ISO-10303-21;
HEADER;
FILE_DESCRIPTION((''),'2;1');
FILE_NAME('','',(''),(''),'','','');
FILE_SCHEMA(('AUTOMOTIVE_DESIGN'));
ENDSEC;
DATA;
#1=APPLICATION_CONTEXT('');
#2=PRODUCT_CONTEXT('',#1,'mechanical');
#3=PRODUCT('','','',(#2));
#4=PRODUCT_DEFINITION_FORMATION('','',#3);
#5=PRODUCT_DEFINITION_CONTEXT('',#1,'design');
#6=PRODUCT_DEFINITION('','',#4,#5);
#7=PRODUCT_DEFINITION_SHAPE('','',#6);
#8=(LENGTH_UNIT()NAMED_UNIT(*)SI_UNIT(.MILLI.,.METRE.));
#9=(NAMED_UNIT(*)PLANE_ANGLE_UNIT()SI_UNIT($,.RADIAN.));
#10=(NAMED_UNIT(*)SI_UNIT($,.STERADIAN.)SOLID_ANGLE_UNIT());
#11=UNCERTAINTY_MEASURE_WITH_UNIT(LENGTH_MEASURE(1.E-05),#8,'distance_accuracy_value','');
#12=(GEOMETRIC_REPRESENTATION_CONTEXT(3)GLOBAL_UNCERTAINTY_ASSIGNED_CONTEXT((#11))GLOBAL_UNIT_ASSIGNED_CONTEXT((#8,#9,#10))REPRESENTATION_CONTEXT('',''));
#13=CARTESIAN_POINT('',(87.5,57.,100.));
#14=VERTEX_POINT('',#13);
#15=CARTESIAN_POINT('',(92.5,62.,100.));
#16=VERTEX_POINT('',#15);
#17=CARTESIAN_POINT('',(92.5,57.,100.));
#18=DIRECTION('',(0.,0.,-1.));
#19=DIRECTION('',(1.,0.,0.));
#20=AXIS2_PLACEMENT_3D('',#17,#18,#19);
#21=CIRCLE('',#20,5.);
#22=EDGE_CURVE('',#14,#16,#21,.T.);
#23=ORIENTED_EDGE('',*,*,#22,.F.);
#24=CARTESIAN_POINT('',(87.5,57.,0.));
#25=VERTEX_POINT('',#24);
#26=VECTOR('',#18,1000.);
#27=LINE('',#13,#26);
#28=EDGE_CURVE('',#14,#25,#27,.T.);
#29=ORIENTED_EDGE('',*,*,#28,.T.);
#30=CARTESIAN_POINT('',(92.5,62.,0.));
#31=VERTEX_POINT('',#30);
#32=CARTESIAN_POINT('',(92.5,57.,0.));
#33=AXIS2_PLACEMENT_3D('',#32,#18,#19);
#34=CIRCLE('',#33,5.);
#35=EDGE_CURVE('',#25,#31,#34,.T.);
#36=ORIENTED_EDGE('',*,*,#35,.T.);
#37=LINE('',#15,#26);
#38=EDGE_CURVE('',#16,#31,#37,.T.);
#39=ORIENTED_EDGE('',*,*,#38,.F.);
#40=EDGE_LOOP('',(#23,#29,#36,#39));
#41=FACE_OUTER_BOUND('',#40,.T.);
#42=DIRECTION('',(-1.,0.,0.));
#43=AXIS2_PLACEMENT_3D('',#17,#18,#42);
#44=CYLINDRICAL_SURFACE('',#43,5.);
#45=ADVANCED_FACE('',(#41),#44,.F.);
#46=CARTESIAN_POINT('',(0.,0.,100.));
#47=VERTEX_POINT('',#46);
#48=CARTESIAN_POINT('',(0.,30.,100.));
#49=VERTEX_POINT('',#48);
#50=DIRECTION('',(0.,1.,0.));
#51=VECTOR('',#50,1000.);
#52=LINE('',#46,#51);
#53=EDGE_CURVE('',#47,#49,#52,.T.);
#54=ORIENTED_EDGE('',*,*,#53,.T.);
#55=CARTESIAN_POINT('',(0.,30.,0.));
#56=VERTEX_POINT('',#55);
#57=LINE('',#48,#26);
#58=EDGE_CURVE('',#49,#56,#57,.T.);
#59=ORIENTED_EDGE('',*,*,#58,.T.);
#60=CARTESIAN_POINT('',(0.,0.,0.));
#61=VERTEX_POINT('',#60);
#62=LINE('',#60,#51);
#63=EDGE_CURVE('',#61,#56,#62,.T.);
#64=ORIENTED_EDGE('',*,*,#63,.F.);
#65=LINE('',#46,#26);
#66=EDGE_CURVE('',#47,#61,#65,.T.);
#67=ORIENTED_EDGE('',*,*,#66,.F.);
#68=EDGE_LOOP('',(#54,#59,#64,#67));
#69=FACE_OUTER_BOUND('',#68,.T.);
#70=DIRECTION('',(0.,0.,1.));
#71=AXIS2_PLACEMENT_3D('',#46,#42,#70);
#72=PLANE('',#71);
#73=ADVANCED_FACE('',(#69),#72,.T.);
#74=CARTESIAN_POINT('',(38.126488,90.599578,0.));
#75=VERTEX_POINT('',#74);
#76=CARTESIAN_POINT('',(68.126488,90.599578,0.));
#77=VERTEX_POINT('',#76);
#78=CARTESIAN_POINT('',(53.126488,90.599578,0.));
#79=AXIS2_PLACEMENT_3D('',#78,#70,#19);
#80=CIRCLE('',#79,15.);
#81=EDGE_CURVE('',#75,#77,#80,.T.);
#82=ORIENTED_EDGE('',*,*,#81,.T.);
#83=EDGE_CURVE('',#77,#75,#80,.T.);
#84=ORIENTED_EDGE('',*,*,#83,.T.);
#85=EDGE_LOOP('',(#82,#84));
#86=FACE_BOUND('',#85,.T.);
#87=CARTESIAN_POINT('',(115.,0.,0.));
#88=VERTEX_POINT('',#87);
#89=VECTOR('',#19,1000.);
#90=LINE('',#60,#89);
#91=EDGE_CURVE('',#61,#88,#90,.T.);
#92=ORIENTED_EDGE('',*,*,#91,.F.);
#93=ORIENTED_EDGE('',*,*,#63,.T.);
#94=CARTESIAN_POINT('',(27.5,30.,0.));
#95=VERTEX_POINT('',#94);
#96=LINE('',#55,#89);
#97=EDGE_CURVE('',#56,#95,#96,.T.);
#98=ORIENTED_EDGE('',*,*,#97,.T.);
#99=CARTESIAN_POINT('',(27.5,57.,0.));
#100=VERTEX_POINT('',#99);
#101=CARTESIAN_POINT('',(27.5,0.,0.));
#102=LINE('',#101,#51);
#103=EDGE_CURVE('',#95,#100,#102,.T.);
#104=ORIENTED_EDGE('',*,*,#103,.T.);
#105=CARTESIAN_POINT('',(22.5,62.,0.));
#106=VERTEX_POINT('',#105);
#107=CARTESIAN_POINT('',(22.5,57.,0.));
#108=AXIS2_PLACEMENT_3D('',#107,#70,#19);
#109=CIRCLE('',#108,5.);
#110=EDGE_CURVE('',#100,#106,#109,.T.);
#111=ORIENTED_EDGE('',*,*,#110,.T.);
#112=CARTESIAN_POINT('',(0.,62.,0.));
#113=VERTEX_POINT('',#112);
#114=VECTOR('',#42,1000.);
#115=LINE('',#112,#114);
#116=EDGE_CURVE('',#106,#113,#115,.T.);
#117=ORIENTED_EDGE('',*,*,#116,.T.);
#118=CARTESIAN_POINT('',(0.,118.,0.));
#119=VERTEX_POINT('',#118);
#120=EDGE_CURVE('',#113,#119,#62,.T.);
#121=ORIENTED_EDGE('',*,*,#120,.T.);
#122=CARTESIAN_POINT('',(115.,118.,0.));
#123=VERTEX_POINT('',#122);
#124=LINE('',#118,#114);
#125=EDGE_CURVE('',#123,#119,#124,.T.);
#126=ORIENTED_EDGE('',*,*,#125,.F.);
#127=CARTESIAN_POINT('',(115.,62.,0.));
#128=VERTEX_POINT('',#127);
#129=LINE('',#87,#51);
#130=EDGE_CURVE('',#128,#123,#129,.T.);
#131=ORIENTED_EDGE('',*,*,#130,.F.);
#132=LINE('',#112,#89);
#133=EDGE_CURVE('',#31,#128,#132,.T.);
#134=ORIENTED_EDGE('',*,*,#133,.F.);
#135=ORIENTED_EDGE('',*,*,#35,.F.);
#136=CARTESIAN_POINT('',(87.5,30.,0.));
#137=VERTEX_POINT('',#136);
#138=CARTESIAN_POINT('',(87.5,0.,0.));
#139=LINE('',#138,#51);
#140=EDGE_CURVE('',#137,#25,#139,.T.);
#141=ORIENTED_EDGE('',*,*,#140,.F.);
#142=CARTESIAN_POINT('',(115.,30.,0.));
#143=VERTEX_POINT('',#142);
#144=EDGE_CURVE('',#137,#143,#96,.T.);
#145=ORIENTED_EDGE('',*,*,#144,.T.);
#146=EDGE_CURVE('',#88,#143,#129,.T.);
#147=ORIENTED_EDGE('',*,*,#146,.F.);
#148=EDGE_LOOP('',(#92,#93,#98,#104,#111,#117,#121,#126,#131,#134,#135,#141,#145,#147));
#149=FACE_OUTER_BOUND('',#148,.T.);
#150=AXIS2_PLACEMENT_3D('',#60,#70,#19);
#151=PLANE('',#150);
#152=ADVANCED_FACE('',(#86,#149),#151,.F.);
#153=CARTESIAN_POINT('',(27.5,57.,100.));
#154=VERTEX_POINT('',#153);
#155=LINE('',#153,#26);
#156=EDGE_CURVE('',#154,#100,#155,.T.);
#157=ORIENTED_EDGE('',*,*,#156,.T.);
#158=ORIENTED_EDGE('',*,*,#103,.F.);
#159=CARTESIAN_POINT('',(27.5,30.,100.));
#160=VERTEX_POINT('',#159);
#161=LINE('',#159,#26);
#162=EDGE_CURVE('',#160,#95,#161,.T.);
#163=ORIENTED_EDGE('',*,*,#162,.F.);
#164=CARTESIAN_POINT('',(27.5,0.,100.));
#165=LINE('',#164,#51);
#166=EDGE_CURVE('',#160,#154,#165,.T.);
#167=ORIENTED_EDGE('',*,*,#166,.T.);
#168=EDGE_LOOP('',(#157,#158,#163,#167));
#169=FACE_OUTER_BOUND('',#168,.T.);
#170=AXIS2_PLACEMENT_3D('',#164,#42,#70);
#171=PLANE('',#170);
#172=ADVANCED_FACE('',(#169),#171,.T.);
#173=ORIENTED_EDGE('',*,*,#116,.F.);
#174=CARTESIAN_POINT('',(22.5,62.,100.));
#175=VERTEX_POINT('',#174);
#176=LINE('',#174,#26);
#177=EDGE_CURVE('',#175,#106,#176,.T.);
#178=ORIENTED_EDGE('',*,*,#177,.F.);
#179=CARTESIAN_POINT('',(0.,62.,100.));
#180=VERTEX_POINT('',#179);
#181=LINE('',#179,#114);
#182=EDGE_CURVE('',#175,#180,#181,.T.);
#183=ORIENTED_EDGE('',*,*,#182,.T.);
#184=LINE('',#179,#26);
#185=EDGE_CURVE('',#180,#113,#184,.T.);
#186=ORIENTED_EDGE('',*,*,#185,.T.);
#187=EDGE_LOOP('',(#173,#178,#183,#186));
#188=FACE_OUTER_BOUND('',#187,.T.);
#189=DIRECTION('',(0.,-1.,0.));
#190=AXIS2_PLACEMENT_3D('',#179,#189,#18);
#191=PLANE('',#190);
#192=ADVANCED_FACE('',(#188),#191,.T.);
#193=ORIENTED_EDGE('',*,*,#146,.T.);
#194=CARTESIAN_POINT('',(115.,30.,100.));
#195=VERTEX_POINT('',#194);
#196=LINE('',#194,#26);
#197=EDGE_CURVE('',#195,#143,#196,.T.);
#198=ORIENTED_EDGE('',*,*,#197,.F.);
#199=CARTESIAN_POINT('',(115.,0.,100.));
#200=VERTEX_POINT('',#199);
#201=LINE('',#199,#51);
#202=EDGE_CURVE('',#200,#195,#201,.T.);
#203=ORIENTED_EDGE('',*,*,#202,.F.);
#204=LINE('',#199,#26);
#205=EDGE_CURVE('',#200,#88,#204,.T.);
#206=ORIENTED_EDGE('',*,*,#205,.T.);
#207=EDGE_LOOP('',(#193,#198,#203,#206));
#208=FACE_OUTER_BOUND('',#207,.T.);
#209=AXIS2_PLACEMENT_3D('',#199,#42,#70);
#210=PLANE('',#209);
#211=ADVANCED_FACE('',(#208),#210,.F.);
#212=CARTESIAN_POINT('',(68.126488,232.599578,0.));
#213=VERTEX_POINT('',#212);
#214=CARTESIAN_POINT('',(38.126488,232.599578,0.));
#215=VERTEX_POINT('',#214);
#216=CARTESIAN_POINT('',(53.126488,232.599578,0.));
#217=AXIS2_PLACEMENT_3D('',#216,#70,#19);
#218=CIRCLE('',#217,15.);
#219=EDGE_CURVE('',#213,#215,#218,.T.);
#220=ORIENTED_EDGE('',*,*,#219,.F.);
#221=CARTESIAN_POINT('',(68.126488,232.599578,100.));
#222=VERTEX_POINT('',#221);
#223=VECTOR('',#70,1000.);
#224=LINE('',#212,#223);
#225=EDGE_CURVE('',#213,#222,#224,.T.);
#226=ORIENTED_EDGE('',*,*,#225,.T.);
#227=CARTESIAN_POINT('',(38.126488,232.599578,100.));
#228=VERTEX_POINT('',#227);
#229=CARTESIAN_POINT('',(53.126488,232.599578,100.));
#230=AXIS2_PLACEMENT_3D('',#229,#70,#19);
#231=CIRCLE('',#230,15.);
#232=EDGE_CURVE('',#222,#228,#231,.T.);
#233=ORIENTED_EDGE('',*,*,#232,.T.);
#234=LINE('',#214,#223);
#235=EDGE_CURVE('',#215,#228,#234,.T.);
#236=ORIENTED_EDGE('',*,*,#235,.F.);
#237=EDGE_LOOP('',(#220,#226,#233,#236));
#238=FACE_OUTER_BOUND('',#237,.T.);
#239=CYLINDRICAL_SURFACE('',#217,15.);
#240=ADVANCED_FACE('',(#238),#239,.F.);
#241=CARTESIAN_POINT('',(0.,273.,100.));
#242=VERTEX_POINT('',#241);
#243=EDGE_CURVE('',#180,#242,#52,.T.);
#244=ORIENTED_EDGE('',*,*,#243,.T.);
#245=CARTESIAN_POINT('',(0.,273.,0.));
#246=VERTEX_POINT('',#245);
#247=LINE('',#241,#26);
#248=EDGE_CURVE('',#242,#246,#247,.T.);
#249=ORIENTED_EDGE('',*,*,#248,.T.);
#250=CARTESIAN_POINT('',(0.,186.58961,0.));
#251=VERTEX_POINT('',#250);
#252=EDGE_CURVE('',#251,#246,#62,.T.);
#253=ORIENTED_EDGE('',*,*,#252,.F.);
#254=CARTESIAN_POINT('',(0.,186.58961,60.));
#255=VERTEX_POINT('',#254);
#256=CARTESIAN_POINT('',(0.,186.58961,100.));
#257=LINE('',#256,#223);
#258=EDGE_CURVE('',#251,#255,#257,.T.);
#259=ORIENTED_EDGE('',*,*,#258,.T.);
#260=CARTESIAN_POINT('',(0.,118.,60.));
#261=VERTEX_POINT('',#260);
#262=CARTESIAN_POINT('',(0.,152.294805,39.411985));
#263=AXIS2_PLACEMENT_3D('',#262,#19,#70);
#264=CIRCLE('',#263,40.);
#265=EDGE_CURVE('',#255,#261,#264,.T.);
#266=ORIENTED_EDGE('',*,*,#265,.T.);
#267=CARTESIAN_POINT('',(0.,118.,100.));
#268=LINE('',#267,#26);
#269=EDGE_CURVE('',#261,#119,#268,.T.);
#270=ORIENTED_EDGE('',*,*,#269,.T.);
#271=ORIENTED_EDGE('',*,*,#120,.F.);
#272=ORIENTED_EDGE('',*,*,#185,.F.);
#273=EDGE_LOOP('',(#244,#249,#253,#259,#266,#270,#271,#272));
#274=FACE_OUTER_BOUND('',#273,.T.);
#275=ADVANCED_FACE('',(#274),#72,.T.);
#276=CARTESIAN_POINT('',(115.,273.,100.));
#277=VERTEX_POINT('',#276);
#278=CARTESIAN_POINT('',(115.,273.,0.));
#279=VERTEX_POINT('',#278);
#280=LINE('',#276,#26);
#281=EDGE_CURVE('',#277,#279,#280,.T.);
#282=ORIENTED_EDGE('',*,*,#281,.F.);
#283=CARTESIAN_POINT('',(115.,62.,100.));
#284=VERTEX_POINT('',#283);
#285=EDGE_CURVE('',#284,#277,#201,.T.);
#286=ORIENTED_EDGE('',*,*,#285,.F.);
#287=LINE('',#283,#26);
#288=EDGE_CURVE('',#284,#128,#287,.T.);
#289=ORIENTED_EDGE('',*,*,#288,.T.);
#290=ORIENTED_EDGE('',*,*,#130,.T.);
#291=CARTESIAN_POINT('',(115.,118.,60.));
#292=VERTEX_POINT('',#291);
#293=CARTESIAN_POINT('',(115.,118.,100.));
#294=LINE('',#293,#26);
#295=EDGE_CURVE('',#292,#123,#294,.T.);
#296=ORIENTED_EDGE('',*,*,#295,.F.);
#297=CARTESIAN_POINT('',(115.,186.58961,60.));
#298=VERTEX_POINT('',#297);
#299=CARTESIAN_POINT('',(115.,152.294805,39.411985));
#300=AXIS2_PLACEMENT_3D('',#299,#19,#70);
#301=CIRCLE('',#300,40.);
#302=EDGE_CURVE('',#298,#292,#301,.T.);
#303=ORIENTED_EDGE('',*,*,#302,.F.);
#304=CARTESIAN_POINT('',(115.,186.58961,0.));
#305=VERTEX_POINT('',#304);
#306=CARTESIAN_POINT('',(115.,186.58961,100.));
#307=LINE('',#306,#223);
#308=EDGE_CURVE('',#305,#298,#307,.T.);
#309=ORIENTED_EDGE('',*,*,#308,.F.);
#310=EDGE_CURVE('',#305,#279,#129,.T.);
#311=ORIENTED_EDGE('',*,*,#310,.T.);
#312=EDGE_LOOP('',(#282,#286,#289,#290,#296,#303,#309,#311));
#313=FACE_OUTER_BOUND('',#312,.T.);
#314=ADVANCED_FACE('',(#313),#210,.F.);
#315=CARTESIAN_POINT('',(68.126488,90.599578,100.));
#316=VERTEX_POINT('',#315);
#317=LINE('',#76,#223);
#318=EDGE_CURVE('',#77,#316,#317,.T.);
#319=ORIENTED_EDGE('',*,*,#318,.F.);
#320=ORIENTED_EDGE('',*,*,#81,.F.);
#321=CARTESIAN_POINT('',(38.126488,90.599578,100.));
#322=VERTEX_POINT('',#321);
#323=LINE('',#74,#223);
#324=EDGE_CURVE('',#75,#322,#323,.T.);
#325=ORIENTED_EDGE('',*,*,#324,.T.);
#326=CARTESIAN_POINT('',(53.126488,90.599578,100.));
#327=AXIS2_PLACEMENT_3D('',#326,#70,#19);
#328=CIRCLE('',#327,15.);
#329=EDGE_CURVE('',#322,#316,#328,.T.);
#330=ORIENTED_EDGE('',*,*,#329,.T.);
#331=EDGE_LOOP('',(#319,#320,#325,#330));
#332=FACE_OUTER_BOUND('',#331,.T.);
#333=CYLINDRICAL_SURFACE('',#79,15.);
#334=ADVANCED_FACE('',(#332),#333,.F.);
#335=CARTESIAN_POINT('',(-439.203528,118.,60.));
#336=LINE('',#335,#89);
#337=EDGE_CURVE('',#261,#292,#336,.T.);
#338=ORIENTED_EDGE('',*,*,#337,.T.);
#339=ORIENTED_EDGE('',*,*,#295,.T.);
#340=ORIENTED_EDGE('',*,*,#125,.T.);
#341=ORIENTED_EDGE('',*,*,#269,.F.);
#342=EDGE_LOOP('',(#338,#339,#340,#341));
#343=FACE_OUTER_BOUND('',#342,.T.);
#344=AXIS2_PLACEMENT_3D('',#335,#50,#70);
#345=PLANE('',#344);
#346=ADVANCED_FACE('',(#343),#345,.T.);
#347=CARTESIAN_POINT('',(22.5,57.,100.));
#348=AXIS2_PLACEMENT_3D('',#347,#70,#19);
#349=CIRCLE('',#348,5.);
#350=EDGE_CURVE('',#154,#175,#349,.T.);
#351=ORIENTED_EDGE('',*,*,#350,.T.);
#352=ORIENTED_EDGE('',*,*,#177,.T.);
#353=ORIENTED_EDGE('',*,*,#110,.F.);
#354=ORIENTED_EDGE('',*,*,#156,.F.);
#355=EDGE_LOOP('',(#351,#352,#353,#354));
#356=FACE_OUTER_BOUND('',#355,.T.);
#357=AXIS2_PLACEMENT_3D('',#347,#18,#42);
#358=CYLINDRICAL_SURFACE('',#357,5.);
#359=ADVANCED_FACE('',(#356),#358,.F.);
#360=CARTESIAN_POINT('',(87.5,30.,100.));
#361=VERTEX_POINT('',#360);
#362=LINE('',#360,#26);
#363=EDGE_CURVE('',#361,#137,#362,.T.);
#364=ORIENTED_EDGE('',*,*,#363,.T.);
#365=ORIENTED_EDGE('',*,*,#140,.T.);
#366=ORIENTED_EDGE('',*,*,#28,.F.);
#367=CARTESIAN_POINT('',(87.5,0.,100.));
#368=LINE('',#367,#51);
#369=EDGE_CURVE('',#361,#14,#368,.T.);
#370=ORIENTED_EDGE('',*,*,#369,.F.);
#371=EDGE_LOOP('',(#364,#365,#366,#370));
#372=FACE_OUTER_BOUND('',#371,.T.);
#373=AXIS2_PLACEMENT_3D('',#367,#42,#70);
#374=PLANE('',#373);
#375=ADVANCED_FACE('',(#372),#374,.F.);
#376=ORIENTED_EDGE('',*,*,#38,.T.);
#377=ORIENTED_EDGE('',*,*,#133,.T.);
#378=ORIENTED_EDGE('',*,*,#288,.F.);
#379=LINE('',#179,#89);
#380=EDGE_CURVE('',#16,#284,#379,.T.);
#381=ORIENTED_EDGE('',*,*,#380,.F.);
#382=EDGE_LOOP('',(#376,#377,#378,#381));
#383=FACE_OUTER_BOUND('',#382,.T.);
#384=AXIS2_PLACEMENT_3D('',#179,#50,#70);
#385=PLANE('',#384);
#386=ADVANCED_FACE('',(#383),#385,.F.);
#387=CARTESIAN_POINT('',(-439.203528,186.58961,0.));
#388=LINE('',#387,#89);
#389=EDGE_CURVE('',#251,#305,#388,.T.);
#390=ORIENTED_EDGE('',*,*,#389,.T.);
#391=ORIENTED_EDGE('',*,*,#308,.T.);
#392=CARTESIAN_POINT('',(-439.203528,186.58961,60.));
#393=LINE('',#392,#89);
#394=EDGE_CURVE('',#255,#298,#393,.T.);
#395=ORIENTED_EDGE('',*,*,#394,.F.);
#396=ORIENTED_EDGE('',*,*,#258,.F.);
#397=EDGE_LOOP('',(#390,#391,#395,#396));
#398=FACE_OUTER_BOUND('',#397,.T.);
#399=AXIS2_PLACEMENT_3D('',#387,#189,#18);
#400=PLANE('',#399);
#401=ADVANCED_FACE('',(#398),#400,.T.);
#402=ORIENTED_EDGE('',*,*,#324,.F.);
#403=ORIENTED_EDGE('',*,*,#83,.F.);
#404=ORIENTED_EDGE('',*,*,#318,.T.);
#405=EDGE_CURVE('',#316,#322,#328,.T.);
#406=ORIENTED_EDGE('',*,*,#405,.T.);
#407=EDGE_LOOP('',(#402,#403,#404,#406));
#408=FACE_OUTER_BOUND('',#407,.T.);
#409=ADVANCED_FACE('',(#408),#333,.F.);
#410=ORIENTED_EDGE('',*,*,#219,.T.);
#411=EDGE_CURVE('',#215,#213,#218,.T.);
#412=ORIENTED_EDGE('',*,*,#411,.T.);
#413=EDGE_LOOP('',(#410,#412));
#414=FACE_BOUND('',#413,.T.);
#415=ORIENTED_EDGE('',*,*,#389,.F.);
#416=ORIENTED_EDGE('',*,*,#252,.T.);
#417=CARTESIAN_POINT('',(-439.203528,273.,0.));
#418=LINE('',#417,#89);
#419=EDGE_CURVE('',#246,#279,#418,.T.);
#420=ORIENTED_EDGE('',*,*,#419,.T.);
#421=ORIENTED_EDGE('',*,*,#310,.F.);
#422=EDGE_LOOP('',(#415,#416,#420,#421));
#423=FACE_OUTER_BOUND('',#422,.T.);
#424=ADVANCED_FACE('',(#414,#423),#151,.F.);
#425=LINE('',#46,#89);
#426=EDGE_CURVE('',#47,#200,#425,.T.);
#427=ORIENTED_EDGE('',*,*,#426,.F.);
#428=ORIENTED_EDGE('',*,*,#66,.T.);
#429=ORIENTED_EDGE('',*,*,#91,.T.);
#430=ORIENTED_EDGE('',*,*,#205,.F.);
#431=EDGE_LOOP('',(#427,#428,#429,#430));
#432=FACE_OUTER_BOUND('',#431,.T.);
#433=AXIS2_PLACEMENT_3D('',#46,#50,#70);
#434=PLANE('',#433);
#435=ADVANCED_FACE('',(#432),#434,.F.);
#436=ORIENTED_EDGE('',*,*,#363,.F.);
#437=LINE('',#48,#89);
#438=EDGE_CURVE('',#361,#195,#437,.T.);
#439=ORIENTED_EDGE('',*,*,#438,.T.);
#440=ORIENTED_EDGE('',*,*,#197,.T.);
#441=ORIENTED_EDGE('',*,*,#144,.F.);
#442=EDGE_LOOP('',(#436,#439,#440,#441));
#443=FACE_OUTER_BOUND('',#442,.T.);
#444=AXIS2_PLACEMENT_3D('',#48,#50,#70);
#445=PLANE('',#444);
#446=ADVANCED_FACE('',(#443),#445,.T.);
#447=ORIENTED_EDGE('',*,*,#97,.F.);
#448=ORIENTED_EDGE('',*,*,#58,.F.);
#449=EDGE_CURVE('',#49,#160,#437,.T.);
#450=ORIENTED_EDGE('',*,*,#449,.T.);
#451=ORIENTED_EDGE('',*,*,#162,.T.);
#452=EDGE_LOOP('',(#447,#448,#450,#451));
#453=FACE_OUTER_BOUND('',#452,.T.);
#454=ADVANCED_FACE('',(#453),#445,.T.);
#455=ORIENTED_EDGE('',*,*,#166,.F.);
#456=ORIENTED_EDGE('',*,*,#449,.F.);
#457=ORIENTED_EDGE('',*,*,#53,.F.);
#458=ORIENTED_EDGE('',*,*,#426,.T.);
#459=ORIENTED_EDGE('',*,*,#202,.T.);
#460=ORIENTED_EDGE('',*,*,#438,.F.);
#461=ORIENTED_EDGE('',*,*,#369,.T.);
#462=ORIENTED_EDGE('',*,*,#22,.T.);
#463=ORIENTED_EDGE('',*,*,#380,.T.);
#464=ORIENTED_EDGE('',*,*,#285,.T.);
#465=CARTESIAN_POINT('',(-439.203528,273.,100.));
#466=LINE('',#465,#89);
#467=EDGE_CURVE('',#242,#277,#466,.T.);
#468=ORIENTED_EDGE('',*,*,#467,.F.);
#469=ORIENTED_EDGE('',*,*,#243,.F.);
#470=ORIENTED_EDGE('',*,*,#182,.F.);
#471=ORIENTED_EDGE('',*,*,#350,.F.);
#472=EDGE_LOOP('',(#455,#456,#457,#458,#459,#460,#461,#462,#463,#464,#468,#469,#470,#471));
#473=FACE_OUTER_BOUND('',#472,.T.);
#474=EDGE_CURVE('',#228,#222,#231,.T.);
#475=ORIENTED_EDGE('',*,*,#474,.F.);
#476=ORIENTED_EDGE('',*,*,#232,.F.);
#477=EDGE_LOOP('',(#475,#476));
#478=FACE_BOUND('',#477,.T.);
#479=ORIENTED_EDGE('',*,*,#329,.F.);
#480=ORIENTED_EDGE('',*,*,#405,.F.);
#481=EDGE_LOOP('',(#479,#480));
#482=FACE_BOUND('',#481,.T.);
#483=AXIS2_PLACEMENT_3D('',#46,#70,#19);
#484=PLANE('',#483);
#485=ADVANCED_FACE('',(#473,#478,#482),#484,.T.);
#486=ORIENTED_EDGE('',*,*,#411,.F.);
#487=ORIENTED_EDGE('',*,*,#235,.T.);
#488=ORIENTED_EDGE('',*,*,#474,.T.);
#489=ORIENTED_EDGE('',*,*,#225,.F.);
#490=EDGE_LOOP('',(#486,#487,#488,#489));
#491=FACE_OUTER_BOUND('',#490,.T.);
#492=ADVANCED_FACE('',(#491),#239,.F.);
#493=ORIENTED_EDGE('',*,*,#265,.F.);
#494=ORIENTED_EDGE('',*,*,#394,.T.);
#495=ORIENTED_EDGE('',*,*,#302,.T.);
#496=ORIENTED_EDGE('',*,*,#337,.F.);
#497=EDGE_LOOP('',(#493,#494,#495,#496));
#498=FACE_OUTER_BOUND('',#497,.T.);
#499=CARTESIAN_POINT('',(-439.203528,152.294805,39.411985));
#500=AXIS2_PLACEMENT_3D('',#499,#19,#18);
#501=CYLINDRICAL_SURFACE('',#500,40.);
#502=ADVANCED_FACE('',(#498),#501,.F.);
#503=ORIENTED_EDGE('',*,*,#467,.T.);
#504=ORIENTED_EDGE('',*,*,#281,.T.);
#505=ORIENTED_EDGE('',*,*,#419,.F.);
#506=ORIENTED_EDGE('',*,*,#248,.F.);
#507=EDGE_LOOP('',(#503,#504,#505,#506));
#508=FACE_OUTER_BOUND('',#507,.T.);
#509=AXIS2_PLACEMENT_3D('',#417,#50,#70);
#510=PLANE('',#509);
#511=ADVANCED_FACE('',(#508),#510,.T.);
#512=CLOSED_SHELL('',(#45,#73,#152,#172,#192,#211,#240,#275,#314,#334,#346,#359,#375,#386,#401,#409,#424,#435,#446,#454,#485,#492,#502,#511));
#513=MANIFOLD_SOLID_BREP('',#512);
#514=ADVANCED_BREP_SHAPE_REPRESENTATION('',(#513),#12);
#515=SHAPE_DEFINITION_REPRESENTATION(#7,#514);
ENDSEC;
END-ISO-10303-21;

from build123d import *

# Parameters (mm, degrees)
SUPPORT_PROFILE_SKETCH_W         = 115
SUPPORT_PROFILE_SKETCH_H         = 30
SUPPORT_BODY_DEPTH               = 100
SIDE_MOUNTING_HOLES_SKETCH_R     = 15
SIDE_MOUNTING_HOLES_2X_DEPTH     = 324.8628221
OPEN_BEARING_SEAT_CUT_DEPTH      = 324.8628221
OPEN_BEARING_SEAT_CUT_DEPTH_BACK = 324.8628221


with BuildPart() as part:
    # Support Profile Sketch → Support Body (new body)
    with BuildSketch(Plane.XY):
        with BuildLine():
            Line((27.5, 57), (27.5, 30))
            Line((27.5, 30), (57.5, 30))
            Line((57.5, 30), (87.5, 30))
            Line((87.5, 30), (87.5, 57))
            ThreePointArc((87.5, 57), (88.964466094, 60.535533906), (92.5, 62))
            Line((92.5, 62), (115, 62))
            Line((115, 62), (115, 273))
            ThreePointArc((115, 273), (57.5, 285.765861395), (0, 273))
            Line((0, 273), (0, 62))
            Line((0, 62), (22.5, 62))
            ThreePointArc((22.5, 62), (26.035533906, 60.535533906), (27.5, 57))
        make_face()
        with Locations((57.5, 15)):
            Rectangle(SUPPORT_PROFILE_SKETCH_W, SUPPORT_PROFILE_SKETCH_H)
    extrude(amount=SUPPORT_BODY_DEPTH)

    # Side Mounting Holes Sketch → Side Mounting Holes 2x (cut, through all)
    with BuildSketch(Plane.XY.offset(100)):
        with Locations((53.126487568, 232.599577538)):
            Circle(SIDE_MOUNTING_HOLES_SKETCH_R)
        with Locations((53.126487568, 90.599577538)):
            Circle(SIDE_MOUNTING_HOLES_SKETCH_R)
    extrude(amount=-SIDE_MOUNTING_HOLES_2X_DEPTH, mode=Mode.SUBTRACT)

    # Bearing Seat Sketch → Open Bearing Seat Cut (cut, two sides: drawn at the far end of the back side and taken through both)
    with BuildSketch(Plane.ZY.offset(-OPEN_BEARING_SEAT_CUT_DEPTH_BACK)):
        with BuildLine():
            Line((-500.188374916, 118), (0, 118))
            Line((0, 118), (60, 118))
            ThreePointArc((60, 118), (79.41198533, 152.294805029), (60, 186.589610057))
            Line((60, 186.589610057), (0, 186.589610057))
            Line((0, 186.589610057), (0, 273))
            Line((0, 273), (100, 273))
            Line((100, 273), (100, 180.5))
            Line((100, 180.5), (108, 180.5))
            Line((108, 180.5), (108, 135.5))
            Line((108, 135.5), (100, 135.5))
            Line((100, 135.5), (100, 62))
            Line((100, 62), (100, -438.188374916))
            Line((100, -438.188374916), (779.965669758, 295.569302764))
            Line((779.965669758, 295.569302764), (179.777294842, 851.75767768))
            Line((179.777294842, 851.75767768), (-500.188374916, 118))
        make_face()
    extrude(amount=OPEN_BEARING_SEAT_CUT_DEPTH + OPEN_BEARING_SEAT_CUT_DEPTH_BACK, mode=Mode.SUBTRACT)


solid = part.part
